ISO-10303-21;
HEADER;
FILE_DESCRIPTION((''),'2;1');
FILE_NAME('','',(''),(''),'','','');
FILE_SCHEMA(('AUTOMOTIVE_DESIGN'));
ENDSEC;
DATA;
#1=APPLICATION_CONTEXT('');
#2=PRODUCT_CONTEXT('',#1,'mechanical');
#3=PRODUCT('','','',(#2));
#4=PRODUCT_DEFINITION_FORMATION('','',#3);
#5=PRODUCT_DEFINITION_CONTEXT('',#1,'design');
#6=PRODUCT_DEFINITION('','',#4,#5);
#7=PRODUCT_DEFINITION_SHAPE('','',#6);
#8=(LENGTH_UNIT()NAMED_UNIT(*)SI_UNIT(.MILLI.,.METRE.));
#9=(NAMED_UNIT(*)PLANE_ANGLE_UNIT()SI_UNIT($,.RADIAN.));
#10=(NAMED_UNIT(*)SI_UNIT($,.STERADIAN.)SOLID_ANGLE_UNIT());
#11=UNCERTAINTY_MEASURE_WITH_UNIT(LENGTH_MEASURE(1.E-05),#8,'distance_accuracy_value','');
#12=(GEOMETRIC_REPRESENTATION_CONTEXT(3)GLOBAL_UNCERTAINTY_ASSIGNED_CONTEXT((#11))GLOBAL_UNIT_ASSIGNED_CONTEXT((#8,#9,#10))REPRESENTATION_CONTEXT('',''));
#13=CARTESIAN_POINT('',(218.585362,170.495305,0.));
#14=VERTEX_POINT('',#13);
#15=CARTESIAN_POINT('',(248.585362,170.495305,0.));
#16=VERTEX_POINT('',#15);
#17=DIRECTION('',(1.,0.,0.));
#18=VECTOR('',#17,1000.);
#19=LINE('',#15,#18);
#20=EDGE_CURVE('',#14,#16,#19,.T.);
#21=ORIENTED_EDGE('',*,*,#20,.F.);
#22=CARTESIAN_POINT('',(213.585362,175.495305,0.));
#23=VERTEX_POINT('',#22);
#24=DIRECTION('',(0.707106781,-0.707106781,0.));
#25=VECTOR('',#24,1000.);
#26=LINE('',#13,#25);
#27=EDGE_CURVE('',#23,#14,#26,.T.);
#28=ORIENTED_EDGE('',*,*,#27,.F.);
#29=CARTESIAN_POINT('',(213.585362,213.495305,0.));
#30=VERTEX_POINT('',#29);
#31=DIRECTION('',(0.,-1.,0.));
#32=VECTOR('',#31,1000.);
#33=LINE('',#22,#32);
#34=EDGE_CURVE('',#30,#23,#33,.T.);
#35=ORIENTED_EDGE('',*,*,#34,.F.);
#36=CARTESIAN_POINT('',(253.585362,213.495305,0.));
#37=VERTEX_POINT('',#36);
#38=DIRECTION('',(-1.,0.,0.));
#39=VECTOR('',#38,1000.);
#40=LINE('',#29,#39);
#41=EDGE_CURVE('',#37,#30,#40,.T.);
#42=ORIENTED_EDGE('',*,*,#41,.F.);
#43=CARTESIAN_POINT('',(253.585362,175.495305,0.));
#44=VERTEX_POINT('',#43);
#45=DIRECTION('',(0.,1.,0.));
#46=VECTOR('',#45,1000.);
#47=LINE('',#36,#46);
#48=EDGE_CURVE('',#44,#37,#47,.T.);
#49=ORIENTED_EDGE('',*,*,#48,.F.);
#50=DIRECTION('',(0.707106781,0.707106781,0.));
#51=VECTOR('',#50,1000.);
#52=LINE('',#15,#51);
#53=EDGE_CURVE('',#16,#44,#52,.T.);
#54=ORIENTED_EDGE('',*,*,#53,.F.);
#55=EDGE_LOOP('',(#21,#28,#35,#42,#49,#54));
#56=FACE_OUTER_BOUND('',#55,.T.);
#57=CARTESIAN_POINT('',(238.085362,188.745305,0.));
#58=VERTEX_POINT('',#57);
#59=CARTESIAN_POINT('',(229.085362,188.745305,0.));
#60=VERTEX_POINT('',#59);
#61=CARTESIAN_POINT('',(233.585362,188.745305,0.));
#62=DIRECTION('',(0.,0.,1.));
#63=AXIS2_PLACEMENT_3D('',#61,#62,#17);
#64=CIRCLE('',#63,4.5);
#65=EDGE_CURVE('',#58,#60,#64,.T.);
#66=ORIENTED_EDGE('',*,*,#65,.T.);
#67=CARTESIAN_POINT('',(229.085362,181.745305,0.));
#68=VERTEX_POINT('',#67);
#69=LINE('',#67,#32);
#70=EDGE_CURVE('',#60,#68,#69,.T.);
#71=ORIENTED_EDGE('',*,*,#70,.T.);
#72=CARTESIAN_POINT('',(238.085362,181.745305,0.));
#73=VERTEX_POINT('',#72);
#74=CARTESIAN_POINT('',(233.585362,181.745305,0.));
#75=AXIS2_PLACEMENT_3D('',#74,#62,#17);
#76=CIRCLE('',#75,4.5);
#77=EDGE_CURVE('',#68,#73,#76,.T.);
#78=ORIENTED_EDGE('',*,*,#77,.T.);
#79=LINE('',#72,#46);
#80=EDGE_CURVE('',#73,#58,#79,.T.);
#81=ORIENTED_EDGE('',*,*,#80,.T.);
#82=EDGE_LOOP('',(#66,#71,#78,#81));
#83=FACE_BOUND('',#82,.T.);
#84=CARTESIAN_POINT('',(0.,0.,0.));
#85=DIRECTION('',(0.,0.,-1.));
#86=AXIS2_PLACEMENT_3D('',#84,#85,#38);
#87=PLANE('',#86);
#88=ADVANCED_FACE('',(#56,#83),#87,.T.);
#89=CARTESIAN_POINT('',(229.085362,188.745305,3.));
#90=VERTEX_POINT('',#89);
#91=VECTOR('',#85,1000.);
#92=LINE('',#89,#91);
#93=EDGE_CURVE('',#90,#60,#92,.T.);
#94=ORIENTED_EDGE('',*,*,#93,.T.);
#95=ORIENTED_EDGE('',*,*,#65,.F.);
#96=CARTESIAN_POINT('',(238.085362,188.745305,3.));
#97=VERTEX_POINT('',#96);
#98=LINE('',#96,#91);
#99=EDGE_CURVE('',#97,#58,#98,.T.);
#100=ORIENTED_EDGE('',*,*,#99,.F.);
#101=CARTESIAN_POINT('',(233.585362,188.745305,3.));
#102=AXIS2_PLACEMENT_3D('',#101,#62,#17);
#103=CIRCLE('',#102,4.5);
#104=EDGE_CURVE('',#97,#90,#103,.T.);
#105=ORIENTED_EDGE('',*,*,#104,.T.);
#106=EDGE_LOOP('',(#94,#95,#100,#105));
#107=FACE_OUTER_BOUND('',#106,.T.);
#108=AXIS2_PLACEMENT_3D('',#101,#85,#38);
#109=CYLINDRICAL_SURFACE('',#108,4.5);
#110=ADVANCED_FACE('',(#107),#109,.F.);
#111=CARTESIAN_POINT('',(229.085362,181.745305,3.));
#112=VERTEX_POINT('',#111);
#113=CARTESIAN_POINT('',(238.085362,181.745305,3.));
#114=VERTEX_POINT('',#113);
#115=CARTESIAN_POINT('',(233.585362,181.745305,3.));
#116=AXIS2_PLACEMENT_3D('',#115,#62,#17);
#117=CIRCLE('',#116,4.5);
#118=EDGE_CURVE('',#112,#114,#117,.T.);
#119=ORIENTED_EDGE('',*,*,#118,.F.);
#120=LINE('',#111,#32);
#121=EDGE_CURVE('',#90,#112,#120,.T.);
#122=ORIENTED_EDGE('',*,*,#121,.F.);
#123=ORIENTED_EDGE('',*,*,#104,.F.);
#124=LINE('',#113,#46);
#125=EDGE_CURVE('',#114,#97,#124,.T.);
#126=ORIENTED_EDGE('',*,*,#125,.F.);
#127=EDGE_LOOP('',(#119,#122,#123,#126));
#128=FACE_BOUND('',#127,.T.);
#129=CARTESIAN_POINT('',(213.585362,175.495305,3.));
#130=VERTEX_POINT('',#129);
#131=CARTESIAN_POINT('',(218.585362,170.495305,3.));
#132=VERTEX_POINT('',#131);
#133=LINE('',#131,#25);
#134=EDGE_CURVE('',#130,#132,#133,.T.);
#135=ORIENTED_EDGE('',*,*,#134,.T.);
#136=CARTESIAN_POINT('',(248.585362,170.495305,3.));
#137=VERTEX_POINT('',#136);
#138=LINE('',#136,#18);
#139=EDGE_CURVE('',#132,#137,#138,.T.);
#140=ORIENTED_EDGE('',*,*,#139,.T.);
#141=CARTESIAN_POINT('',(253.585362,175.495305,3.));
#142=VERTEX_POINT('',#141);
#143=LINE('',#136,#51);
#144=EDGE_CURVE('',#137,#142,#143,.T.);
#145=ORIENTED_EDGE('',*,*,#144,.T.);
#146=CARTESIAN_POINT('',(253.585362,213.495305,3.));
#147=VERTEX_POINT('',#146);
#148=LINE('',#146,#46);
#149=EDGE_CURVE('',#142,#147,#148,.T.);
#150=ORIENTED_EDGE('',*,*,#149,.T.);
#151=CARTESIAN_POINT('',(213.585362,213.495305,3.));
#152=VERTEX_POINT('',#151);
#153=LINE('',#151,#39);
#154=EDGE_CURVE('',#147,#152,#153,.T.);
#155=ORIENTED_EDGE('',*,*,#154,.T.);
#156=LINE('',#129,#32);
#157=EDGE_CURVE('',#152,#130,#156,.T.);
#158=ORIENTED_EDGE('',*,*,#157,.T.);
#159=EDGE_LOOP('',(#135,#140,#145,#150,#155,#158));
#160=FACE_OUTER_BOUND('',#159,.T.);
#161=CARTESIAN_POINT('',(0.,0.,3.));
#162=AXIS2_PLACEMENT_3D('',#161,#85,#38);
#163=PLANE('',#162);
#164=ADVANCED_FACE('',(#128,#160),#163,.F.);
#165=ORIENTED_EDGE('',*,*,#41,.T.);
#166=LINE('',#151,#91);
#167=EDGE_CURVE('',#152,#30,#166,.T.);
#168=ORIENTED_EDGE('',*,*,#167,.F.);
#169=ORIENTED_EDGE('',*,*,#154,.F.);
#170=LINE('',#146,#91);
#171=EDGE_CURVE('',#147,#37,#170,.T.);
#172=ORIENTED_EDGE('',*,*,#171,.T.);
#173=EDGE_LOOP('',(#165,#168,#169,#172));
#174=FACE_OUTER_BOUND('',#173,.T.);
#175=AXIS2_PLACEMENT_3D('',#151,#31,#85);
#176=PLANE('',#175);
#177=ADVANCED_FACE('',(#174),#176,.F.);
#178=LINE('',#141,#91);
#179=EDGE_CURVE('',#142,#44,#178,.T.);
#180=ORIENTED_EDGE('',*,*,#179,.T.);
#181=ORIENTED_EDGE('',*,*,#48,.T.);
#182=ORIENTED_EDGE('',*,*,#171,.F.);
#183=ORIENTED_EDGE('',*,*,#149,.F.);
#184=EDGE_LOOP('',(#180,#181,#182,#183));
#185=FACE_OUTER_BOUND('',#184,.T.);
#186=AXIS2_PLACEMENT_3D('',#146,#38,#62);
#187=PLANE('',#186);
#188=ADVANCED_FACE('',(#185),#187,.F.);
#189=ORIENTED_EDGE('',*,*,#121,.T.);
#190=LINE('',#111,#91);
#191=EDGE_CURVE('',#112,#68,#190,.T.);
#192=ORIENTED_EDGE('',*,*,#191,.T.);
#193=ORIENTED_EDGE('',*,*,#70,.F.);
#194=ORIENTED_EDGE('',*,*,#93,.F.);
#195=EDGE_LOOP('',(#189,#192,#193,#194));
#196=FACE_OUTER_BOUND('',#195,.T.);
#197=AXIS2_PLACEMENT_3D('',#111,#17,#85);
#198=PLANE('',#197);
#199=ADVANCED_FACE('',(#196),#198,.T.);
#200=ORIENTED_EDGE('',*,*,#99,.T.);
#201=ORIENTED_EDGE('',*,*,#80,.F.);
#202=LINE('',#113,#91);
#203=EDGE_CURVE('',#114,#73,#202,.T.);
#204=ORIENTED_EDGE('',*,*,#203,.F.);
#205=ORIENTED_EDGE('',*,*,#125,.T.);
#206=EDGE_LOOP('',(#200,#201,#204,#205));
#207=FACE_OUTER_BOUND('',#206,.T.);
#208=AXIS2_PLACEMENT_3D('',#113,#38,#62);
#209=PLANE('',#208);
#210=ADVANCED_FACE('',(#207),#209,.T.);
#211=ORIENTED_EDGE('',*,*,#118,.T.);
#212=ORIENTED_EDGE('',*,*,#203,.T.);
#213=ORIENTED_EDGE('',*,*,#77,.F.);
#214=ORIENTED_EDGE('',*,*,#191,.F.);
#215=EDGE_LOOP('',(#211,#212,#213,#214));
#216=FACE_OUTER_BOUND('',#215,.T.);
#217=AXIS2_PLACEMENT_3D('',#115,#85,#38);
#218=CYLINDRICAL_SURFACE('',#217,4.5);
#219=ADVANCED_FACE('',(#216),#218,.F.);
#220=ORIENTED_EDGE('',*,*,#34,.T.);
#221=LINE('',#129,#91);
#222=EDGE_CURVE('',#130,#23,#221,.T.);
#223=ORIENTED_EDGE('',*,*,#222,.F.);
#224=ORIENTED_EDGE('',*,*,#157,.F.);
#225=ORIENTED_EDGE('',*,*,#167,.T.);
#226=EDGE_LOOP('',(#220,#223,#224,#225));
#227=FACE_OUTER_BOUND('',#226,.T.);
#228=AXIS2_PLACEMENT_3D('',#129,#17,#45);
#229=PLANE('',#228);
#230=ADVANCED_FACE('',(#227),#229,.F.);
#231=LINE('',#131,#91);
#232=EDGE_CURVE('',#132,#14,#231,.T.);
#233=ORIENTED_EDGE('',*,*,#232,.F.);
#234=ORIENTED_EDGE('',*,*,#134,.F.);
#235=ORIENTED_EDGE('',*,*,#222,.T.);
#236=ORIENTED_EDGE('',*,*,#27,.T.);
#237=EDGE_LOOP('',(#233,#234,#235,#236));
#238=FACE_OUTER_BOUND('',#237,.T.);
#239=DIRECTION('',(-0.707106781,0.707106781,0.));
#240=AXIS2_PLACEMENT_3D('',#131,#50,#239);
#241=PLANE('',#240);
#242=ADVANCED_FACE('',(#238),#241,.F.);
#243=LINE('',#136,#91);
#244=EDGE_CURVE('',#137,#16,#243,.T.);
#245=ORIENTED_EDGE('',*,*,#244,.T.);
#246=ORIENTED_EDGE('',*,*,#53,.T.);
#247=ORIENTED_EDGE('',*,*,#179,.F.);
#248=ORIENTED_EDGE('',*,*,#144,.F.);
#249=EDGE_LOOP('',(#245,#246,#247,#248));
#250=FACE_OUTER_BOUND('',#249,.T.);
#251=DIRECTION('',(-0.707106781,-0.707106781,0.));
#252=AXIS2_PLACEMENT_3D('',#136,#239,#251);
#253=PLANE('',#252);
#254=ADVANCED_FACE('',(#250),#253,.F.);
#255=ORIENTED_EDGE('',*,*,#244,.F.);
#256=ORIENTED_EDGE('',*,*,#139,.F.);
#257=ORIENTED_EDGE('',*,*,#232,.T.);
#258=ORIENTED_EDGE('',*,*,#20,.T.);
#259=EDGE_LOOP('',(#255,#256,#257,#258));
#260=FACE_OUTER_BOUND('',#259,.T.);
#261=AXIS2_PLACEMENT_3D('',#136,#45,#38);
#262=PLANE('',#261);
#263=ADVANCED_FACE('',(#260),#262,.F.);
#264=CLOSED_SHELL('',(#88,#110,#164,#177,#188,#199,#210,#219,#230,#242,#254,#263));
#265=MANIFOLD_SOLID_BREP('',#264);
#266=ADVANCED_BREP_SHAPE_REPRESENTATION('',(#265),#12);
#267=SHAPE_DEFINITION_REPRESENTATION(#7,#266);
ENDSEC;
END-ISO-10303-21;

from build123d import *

# Parameters (mm, degrees)
BOSS_EXTRUDE1_DEPTH = 3


with BuildPart() as part:
    # Sketch1 → Boss-Extrude1 (new body)
    with BuildSketch(Plane.XY):
        Polygon((213.585362106, 213.495304552), (253.585362106, 213.495304552), (253.585362106, 175.495304552), (248.585362106, 170.495304552), (218.585362106, 170.495304552), (213.585362106, 175.495304552), align=None)
        with BuildLine():
            Line((229.085362106, 181.745304552), (229.085362106, 188.745304552))
            ThreePointArc((229.085362106, 188.745304552), (233.585362106, 193.245304552), (238.085362106, 188.745304552))
            Line((238.085362106, 188.745304552), (238.085362106, 181.745304552))
            ThreePointArc((238.085362106, 181.745304552), (233.585362106, 177.245304552), (229.085362106, 181.745304552))
        make_face(mode=Mode.SUBTRACT)
    extrude(amount=BOSS_EXTRUDE1_DEPTH)


solid = part.part
